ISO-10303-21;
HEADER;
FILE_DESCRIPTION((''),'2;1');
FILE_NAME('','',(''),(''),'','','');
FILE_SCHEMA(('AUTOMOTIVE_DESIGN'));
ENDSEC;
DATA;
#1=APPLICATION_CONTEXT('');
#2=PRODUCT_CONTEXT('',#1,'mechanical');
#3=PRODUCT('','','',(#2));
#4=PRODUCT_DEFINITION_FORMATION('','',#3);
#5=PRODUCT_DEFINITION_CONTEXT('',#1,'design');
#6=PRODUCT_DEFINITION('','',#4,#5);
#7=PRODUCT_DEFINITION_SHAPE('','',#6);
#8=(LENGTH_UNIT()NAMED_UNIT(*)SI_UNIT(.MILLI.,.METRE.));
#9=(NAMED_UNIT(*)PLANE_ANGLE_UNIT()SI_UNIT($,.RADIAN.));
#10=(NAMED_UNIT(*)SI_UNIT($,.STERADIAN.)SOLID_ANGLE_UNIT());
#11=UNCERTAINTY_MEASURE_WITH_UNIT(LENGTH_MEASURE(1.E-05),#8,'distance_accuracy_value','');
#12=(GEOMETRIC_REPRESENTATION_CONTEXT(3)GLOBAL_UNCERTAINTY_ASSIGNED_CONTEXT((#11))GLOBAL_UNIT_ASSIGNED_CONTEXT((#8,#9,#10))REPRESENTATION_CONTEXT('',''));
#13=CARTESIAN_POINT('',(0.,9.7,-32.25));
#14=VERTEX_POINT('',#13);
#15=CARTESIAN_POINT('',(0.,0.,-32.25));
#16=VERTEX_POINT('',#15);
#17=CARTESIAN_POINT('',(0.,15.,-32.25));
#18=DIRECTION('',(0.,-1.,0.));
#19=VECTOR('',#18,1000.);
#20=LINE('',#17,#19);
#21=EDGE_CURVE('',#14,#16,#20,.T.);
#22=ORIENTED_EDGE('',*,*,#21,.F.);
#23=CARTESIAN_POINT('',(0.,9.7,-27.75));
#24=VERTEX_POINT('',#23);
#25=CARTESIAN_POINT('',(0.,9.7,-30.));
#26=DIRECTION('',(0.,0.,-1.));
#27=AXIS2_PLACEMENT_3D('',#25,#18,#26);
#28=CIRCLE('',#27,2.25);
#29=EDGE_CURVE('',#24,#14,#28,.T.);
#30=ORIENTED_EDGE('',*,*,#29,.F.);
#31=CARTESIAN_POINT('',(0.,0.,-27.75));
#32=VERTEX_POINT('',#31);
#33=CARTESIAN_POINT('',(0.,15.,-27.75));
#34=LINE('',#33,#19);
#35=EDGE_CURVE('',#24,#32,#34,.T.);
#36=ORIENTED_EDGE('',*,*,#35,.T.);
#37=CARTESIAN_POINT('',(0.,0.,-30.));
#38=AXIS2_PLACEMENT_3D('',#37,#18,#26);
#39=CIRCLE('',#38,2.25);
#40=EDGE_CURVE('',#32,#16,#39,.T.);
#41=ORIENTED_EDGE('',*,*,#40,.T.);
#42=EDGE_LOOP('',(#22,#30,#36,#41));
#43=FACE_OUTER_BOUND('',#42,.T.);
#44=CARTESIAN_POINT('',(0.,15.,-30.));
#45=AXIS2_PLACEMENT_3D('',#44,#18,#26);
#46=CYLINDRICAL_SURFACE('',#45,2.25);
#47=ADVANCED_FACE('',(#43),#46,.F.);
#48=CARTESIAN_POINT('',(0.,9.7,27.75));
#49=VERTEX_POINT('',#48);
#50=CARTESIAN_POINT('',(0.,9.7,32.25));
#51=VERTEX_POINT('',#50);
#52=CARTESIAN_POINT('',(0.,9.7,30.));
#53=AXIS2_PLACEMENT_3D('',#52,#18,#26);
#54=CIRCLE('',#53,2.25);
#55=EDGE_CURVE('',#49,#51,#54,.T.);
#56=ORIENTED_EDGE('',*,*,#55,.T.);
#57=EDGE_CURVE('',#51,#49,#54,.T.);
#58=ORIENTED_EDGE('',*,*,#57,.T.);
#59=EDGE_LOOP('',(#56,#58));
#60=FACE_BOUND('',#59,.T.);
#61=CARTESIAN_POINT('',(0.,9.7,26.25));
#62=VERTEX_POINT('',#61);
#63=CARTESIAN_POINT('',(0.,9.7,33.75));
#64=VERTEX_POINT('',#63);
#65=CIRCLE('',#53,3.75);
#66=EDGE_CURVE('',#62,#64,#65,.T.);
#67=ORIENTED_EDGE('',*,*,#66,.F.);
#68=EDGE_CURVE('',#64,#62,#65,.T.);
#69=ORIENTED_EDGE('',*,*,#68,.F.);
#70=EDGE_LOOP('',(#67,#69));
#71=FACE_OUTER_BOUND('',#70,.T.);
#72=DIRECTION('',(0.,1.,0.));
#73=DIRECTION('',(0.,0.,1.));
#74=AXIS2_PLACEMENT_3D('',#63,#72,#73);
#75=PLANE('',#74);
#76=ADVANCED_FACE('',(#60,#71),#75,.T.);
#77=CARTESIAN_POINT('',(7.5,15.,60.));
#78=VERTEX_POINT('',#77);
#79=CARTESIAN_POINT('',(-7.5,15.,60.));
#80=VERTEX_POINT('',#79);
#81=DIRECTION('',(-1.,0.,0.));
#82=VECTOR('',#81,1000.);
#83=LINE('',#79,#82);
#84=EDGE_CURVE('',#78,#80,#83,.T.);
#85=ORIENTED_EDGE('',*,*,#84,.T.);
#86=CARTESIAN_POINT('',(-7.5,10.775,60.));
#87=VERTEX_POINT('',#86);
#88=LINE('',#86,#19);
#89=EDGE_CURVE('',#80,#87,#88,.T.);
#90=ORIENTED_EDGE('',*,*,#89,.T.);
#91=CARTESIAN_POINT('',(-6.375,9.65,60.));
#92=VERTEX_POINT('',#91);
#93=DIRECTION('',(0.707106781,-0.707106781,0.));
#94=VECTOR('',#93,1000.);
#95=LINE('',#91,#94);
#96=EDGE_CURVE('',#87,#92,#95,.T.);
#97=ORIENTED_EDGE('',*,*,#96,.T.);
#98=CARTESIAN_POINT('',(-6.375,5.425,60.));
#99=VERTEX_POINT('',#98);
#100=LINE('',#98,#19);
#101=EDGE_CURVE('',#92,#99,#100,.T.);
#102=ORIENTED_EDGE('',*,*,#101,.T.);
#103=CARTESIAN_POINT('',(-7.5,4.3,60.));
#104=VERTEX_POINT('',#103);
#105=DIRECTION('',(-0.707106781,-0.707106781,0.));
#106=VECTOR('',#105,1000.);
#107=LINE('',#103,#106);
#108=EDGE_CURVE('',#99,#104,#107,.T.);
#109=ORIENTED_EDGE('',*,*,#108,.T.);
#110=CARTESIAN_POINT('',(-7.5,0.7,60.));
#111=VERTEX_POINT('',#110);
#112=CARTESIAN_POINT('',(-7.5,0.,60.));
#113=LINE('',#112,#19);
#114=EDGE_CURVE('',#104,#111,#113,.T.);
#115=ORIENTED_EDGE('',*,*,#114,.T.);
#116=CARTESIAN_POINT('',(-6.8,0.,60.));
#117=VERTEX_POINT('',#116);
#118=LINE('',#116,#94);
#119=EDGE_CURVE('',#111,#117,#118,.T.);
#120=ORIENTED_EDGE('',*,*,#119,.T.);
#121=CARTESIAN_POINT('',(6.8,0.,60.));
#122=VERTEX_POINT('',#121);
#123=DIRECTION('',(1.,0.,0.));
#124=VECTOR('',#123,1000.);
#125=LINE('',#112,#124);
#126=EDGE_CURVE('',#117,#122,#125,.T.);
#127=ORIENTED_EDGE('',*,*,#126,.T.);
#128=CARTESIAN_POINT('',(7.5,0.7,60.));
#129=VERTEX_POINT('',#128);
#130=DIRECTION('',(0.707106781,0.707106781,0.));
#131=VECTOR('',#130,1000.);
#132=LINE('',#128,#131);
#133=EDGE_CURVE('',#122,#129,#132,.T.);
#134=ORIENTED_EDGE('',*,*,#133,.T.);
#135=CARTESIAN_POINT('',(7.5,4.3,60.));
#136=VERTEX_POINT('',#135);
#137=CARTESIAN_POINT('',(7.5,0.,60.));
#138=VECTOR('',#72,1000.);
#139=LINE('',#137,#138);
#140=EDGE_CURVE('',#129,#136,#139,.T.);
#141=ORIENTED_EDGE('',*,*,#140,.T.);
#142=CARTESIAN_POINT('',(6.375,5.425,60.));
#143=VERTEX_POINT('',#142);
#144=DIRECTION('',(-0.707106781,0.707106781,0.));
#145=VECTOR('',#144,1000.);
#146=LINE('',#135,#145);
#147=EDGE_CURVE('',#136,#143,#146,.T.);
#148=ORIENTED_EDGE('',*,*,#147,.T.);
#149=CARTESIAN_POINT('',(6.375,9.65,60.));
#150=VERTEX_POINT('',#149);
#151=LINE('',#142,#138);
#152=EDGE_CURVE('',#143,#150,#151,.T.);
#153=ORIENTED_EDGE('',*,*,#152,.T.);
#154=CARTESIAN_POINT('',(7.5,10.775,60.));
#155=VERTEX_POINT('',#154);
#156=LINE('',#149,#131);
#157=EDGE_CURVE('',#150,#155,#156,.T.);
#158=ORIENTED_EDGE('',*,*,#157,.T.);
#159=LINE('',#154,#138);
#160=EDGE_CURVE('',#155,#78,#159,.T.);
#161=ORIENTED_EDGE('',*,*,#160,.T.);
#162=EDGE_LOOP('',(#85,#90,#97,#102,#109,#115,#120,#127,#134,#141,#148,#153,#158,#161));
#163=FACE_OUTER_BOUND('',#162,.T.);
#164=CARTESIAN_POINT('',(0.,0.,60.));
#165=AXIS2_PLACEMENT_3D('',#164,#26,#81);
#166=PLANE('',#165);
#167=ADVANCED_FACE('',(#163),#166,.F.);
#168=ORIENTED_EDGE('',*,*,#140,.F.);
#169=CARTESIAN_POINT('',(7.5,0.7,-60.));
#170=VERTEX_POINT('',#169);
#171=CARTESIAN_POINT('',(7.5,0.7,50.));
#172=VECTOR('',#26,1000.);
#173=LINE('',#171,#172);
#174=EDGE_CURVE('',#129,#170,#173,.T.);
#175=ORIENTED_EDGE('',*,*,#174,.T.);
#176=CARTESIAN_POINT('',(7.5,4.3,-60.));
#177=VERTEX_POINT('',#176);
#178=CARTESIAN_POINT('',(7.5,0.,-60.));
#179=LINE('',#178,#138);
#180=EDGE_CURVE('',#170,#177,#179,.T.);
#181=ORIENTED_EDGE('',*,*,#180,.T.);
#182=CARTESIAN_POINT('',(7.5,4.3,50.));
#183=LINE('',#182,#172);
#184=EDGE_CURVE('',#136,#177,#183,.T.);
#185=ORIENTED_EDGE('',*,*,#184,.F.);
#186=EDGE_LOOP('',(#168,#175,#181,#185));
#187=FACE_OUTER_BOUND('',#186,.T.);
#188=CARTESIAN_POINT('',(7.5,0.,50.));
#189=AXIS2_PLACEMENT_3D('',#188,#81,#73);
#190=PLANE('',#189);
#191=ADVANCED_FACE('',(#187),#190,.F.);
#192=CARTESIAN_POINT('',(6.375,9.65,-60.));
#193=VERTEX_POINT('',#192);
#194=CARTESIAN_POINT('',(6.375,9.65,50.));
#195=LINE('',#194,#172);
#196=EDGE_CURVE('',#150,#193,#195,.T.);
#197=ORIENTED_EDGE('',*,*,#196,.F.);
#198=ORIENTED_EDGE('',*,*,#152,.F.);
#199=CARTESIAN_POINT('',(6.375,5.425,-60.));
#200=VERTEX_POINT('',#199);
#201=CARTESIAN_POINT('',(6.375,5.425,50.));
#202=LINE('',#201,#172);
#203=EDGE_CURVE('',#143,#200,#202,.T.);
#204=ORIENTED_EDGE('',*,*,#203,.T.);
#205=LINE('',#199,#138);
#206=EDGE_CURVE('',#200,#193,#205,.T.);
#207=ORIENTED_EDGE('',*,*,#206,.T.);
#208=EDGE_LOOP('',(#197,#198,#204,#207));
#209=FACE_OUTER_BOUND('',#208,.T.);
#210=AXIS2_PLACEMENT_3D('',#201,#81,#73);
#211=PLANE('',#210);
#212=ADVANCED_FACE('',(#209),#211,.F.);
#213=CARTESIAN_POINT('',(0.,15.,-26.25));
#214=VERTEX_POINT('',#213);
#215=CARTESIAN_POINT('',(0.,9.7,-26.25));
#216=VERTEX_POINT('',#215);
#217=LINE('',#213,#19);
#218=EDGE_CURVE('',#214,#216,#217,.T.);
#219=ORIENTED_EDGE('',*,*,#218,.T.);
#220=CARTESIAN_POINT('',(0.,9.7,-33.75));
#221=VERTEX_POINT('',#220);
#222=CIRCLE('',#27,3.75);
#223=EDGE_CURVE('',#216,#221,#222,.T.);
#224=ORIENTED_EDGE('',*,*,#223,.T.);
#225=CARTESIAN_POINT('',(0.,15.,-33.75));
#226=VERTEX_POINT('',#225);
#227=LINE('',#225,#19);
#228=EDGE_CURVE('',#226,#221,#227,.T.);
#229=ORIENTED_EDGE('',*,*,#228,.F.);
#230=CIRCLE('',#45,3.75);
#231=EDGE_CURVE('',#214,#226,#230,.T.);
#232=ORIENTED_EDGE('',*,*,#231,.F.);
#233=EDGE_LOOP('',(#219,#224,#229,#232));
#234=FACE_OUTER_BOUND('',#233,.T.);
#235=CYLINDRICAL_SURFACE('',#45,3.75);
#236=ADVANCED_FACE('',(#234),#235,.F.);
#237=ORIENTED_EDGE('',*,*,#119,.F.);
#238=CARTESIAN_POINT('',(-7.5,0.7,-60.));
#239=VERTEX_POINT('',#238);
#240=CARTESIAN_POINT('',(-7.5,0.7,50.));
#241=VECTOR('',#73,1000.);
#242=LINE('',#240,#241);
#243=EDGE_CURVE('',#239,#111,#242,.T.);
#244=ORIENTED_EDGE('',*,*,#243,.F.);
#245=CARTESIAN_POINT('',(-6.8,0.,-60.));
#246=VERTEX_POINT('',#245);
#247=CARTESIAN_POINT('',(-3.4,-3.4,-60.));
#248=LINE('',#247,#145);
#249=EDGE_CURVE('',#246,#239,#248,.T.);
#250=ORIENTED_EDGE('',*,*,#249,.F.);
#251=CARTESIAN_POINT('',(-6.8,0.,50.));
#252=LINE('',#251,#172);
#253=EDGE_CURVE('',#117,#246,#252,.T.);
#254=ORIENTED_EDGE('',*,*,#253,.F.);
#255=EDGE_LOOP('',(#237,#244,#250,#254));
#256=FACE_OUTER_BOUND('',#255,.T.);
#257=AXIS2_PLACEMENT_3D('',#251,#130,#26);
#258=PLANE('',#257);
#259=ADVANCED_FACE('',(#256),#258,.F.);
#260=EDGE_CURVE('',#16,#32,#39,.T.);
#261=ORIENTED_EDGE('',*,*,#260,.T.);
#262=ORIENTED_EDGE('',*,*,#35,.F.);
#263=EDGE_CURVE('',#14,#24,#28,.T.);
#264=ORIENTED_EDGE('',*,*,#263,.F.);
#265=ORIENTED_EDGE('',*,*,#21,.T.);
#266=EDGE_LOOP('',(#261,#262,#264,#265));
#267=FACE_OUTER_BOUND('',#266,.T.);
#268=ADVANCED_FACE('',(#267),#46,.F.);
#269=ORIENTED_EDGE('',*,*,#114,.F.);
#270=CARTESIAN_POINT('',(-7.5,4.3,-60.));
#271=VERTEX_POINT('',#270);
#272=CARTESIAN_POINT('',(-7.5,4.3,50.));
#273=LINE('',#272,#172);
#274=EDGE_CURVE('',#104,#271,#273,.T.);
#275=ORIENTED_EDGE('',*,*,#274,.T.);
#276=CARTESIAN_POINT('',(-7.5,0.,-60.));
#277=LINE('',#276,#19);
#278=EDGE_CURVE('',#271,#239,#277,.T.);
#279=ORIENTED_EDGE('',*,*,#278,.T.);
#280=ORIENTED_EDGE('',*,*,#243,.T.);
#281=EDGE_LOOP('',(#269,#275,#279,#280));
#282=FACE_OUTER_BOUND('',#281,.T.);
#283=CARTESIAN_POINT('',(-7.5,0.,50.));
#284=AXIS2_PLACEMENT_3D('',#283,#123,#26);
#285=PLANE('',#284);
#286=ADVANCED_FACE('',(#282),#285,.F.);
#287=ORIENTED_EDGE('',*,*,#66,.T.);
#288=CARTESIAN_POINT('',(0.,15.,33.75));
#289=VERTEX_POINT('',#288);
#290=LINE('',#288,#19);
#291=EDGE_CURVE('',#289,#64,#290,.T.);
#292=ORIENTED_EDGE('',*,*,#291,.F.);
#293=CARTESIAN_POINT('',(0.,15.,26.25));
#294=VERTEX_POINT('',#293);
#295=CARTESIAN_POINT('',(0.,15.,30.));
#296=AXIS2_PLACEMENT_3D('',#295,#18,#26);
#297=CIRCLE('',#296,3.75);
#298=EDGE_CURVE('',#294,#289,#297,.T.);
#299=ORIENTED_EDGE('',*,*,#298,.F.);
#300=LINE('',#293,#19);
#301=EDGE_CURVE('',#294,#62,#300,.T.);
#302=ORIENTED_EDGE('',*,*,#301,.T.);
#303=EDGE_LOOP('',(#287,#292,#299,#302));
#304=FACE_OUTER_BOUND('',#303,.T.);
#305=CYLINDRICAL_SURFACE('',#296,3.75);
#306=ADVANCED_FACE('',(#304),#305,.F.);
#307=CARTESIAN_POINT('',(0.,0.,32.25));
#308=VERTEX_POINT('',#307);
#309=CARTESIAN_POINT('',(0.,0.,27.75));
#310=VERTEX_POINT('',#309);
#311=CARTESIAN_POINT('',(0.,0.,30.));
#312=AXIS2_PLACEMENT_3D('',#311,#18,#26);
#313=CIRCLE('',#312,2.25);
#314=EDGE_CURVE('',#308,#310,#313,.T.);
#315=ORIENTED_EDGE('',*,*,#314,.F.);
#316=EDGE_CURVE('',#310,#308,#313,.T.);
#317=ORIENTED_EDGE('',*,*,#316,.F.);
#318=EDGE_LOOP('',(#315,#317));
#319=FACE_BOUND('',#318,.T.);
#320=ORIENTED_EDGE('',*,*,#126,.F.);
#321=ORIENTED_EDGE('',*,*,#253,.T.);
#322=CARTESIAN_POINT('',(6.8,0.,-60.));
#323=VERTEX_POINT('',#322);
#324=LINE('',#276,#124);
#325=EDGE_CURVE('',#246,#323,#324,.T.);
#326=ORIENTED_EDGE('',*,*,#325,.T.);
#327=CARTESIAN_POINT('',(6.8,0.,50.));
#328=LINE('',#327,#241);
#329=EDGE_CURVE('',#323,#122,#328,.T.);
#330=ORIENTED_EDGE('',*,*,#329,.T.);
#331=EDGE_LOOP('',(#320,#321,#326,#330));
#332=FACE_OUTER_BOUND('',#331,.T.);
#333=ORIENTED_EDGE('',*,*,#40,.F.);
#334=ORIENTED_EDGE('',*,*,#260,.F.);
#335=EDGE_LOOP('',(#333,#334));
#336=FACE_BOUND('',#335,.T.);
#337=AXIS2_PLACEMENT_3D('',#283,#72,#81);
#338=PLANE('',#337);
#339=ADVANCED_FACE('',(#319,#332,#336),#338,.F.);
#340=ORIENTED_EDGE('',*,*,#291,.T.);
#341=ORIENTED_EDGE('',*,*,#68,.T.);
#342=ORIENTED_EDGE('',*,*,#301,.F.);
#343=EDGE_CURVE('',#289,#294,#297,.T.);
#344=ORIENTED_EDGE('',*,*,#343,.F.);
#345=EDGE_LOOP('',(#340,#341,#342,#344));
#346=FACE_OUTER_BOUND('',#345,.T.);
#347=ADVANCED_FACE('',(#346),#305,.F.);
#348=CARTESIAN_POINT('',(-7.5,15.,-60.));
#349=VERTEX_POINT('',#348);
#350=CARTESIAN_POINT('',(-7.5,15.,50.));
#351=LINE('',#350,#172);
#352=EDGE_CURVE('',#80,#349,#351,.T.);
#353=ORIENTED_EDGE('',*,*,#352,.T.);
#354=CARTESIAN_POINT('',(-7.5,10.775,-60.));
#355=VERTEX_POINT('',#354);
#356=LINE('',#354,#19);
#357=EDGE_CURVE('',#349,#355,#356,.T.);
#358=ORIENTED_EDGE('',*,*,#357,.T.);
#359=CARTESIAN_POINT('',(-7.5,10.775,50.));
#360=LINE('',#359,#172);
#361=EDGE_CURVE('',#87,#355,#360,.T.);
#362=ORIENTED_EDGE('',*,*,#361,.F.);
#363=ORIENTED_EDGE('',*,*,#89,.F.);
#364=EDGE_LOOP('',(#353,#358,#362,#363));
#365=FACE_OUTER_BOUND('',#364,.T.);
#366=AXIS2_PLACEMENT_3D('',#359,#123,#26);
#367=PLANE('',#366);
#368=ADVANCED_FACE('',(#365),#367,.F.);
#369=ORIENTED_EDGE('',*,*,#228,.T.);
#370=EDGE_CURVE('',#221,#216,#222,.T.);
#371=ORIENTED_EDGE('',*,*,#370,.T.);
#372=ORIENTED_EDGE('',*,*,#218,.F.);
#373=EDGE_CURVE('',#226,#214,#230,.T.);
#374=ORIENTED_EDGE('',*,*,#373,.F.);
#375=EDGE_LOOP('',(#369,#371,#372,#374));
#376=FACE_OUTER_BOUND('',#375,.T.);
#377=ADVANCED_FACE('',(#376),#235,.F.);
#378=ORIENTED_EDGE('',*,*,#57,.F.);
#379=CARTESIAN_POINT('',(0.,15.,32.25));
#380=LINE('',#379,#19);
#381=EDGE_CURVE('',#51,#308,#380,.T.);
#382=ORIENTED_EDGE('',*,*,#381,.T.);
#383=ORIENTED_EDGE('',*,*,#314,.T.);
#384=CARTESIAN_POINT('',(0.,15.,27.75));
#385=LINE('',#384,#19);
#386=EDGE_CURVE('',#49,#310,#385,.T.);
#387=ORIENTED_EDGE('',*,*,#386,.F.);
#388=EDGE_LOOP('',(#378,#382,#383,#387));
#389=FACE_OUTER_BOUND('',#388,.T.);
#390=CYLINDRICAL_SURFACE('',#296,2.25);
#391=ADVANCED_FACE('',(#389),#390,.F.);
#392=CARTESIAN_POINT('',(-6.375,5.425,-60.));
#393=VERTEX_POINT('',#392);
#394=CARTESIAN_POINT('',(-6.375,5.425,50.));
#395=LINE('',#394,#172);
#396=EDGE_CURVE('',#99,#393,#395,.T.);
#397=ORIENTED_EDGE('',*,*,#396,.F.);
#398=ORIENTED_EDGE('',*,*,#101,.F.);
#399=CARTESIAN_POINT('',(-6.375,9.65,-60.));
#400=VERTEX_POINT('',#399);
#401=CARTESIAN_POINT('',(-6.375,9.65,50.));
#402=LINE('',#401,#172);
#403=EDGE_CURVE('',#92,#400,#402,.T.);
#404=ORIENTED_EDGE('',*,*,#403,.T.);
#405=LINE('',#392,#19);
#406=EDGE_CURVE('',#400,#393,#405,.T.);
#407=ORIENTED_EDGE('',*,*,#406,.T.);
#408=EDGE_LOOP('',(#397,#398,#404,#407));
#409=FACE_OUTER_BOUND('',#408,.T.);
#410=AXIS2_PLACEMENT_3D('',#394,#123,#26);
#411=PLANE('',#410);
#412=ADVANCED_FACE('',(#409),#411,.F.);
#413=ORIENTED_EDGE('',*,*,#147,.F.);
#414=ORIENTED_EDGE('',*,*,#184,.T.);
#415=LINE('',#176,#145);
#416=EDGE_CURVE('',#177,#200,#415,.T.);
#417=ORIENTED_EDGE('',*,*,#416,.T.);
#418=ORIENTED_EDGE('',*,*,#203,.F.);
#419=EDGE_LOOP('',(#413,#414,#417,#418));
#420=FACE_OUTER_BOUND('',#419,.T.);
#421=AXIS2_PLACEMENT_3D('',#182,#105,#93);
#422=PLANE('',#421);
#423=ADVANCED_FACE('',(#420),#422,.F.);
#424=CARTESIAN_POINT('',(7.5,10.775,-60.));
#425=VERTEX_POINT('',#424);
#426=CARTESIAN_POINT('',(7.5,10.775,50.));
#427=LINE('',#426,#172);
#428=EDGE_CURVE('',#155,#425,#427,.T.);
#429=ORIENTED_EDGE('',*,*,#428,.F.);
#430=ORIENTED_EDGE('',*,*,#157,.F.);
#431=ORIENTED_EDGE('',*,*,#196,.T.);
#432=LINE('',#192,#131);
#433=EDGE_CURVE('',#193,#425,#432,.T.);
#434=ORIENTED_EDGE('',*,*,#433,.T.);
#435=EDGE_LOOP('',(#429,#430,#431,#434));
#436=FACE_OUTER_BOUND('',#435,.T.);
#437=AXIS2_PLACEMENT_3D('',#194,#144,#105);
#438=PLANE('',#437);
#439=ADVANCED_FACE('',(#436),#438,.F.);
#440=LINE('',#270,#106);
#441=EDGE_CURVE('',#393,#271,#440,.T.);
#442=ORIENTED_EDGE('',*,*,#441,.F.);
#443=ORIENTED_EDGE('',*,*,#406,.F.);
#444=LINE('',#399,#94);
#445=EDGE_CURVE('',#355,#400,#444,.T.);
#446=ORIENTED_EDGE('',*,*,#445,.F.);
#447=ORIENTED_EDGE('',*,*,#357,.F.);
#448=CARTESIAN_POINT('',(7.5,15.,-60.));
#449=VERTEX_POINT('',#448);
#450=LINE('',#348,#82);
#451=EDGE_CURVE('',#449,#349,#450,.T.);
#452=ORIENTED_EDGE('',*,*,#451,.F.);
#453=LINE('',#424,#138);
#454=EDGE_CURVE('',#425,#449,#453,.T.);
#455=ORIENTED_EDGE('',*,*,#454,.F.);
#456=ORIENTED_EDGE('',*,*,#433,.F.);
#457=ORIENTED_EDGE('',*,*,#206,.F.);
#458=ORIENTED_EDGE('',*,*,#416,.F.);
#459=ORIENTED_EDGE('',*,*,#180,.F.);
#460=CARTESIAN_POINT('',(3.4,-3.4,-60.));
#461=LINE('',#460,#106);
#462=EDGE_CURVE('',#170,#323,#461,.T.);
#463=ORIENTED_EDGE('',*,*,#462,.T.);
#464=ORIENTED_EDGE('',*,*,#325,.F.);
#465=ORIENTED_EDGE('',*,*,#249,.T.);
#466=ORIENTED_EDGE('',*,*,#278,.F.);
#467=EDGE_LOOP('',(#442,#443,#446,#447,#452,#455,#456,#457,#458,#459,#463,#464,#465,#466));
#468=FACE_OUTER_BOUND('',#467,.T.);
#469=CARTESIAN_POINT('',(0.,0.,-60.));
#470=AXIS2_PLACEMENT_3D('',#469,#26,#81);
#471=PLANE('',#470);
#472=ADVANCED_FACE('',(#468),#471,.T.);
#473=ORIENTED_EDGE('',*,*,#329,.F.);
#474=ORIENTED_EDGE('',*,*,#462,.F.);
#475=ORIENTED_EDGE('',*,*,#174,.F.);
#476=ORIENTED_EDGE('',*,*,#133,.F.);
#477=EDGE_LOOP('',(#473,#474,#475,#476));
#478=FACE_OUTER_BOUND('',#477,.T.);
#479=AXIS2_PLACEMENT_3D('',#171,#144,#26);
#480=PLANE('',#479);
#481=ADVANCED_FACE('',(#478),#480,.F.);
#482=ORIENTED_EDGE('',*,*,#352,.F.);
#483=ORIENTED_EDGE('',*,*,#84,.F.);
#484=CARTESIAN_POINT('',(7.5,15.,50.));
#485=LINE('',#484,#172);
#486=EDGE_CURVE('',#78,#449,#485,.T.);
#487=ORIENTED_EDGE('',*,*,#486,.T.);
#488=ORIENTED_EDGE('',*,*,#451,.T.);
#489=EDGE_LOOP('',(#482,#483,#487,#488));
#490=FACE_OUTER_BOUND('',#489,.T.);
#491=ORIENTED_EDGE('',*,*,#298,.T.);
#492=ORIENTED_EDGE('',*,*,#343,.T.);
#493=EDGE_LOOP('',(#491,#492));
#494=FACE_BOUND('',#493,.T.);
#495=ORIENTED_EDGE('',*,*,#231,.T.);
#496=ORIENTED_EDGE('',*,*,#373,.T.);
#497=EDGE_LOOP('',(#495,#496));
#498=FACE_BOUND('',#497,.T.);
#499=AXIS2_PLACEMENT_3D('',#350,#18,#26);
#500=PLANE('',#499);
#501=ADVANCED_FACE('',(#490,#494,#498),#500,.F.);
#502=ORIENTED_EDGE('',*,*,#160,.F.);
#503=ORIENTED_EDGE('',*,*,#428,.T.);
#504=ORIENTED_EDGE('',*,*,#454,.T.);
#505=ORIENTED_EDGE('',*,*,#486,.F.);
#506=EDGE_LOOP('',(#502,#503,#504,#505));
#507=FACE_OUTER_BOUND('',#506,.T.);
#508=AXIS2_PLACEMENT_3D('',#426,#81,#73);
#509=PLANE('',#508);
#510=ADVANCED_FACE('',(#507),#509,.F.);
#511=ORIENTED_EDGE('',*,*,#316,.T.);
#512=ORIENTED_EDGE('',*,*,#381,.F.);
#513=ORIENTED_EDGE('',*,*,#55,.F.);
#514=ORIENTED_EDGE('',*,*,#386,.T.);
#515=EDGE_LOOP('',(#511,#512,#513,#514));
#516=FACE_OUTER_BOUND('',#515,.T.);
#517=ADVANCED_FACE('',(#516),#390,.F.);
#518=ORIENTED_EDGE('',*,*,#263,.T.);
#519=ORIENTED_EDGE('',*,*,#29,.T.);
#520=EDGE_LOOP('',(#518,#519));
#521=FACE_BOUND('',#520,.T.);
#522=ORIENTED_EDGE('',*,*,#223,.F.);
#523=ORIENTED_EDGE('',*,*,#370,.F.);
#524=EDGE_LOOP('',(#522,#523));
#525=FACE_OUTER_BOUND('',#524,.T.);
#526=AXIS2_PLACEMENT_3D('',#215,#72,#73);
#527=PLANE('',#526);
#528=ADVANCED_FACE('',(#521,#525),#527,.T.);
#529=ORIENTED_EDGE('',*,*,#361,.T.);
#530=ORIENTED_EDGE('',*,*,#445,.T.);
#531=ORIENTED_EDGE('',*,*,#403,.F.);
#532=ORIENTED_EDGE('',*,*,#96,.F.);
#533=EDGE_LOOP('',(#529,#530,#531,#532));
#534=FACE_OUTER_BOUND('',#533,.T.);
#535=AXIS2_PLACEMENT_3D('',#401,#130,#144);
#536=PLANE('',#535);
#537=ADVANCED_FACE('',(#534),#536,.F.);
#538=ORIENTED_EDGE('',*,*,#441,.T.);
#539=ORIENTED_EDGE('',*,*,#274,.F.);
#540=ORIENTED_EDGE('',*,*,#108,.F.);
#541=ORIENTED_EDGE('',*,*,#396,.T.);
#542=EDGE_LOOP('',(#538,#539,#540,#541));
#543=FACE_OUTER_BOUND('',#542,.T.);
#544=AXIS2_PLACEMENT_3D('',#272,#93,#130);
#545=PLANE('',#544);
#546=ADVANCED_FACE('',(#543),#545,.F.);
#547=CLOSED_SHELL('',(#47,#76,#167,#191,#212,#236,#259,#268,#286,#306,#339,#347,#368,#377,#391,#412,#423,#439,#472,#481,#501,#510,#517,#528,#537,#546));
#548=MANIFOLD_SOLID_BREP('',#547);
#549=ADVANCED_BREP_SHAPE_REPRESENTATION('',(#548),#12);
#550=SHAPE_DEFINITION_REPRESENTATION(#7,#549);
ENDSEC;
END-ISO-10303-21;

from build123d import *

# Parameters (mm, degrees)
EXTRUDE_1_DEPTH        = 50
CHAMFER_1_SIZE         = 0.7
PATTERN_LINEAR_1_COUNT = 2
PATTERN_LINEAR_1_PITCH = 60
MOVE_FACE_1_BY         = 10
MOVE_FACE_2_BY         = 10


with BuildPart() as part:
    # 草图1 → 凸台-拉伸1 (new, symmetric)
    with BuildSketch(Plane.XY):
        Polygon((-7.5, 0), (7.5, 0), (7.5, 4.3), (6.375, 5.425), (6.375, 9.65), (7.5, 10.775), (7.5, 15), (-7.5, 15), (-7.5, 10.775), (-6.375, 9.65), (-6.375, 5.425), (-7.5, 4.3), align=None)
    extrude(amount=EXTRUDE_1_DEPTH, both=True)

    # 倒角1
    chamfer_1_edges = [part.edges().sort_by_distance(p)[0] for p in [
        (7.5, 0, 0),
        (-7.5, 0, 0),
    ]]
    chamfer(chamfer_1_edges, length=CHAMFER_1_SIZE)

    # 草图3 → Cut-Revolve 1095 (revolve, cut)
    with BuildSketch(Plane(origin=(0, 0, 0), x_dir=(0, 0, -1), z_dir=(1, 0, 0)), mode=Mode.PRIVATE) as cut_revolve_1095_sk:
        Polygon((-30, 15), (-33.75, 15), (-33.75, 9.7), (-32.25, 9.7), (-32.25, 0), (-30, 0), align=None)
    cut_revolve_1095 = revolve(cut_revolve_1095_sk.sketch.rotate(Axis((0, 15, 30), (0, 1, 0)), 180), axis=Axis((0, 15, 30), (0, 1, 0)), mode=Mode.SUBTRACT)

    # 上锁孔阵列(线性)1: Cut-Revolve 1095 ×2
    with Locations(*[(0, 0, -i * PATTERN_LINEAR_1_PITCH) for i in range(1, PATTERN_LINEAR_1_COUNT)]):
        add(cut_revolve_1095, mode=Mode.SUBTRACT)

    # Move Face 1: a face moved outward by 10.0
    extrude(part.faces().sort_by_distance((0, 7.514633707, 50))[0], amount=MOVE_FACE_1_BY, dir=(0, 0, 1))

    # Move Face 2: a face moved outward by 10.0
    extrude(part.faces().sort_by_distance((0, 7.514633707, -50))[0], amount=MOVE_FACE_2_BY, dir=(0, 0, -1))


solid = part.part
